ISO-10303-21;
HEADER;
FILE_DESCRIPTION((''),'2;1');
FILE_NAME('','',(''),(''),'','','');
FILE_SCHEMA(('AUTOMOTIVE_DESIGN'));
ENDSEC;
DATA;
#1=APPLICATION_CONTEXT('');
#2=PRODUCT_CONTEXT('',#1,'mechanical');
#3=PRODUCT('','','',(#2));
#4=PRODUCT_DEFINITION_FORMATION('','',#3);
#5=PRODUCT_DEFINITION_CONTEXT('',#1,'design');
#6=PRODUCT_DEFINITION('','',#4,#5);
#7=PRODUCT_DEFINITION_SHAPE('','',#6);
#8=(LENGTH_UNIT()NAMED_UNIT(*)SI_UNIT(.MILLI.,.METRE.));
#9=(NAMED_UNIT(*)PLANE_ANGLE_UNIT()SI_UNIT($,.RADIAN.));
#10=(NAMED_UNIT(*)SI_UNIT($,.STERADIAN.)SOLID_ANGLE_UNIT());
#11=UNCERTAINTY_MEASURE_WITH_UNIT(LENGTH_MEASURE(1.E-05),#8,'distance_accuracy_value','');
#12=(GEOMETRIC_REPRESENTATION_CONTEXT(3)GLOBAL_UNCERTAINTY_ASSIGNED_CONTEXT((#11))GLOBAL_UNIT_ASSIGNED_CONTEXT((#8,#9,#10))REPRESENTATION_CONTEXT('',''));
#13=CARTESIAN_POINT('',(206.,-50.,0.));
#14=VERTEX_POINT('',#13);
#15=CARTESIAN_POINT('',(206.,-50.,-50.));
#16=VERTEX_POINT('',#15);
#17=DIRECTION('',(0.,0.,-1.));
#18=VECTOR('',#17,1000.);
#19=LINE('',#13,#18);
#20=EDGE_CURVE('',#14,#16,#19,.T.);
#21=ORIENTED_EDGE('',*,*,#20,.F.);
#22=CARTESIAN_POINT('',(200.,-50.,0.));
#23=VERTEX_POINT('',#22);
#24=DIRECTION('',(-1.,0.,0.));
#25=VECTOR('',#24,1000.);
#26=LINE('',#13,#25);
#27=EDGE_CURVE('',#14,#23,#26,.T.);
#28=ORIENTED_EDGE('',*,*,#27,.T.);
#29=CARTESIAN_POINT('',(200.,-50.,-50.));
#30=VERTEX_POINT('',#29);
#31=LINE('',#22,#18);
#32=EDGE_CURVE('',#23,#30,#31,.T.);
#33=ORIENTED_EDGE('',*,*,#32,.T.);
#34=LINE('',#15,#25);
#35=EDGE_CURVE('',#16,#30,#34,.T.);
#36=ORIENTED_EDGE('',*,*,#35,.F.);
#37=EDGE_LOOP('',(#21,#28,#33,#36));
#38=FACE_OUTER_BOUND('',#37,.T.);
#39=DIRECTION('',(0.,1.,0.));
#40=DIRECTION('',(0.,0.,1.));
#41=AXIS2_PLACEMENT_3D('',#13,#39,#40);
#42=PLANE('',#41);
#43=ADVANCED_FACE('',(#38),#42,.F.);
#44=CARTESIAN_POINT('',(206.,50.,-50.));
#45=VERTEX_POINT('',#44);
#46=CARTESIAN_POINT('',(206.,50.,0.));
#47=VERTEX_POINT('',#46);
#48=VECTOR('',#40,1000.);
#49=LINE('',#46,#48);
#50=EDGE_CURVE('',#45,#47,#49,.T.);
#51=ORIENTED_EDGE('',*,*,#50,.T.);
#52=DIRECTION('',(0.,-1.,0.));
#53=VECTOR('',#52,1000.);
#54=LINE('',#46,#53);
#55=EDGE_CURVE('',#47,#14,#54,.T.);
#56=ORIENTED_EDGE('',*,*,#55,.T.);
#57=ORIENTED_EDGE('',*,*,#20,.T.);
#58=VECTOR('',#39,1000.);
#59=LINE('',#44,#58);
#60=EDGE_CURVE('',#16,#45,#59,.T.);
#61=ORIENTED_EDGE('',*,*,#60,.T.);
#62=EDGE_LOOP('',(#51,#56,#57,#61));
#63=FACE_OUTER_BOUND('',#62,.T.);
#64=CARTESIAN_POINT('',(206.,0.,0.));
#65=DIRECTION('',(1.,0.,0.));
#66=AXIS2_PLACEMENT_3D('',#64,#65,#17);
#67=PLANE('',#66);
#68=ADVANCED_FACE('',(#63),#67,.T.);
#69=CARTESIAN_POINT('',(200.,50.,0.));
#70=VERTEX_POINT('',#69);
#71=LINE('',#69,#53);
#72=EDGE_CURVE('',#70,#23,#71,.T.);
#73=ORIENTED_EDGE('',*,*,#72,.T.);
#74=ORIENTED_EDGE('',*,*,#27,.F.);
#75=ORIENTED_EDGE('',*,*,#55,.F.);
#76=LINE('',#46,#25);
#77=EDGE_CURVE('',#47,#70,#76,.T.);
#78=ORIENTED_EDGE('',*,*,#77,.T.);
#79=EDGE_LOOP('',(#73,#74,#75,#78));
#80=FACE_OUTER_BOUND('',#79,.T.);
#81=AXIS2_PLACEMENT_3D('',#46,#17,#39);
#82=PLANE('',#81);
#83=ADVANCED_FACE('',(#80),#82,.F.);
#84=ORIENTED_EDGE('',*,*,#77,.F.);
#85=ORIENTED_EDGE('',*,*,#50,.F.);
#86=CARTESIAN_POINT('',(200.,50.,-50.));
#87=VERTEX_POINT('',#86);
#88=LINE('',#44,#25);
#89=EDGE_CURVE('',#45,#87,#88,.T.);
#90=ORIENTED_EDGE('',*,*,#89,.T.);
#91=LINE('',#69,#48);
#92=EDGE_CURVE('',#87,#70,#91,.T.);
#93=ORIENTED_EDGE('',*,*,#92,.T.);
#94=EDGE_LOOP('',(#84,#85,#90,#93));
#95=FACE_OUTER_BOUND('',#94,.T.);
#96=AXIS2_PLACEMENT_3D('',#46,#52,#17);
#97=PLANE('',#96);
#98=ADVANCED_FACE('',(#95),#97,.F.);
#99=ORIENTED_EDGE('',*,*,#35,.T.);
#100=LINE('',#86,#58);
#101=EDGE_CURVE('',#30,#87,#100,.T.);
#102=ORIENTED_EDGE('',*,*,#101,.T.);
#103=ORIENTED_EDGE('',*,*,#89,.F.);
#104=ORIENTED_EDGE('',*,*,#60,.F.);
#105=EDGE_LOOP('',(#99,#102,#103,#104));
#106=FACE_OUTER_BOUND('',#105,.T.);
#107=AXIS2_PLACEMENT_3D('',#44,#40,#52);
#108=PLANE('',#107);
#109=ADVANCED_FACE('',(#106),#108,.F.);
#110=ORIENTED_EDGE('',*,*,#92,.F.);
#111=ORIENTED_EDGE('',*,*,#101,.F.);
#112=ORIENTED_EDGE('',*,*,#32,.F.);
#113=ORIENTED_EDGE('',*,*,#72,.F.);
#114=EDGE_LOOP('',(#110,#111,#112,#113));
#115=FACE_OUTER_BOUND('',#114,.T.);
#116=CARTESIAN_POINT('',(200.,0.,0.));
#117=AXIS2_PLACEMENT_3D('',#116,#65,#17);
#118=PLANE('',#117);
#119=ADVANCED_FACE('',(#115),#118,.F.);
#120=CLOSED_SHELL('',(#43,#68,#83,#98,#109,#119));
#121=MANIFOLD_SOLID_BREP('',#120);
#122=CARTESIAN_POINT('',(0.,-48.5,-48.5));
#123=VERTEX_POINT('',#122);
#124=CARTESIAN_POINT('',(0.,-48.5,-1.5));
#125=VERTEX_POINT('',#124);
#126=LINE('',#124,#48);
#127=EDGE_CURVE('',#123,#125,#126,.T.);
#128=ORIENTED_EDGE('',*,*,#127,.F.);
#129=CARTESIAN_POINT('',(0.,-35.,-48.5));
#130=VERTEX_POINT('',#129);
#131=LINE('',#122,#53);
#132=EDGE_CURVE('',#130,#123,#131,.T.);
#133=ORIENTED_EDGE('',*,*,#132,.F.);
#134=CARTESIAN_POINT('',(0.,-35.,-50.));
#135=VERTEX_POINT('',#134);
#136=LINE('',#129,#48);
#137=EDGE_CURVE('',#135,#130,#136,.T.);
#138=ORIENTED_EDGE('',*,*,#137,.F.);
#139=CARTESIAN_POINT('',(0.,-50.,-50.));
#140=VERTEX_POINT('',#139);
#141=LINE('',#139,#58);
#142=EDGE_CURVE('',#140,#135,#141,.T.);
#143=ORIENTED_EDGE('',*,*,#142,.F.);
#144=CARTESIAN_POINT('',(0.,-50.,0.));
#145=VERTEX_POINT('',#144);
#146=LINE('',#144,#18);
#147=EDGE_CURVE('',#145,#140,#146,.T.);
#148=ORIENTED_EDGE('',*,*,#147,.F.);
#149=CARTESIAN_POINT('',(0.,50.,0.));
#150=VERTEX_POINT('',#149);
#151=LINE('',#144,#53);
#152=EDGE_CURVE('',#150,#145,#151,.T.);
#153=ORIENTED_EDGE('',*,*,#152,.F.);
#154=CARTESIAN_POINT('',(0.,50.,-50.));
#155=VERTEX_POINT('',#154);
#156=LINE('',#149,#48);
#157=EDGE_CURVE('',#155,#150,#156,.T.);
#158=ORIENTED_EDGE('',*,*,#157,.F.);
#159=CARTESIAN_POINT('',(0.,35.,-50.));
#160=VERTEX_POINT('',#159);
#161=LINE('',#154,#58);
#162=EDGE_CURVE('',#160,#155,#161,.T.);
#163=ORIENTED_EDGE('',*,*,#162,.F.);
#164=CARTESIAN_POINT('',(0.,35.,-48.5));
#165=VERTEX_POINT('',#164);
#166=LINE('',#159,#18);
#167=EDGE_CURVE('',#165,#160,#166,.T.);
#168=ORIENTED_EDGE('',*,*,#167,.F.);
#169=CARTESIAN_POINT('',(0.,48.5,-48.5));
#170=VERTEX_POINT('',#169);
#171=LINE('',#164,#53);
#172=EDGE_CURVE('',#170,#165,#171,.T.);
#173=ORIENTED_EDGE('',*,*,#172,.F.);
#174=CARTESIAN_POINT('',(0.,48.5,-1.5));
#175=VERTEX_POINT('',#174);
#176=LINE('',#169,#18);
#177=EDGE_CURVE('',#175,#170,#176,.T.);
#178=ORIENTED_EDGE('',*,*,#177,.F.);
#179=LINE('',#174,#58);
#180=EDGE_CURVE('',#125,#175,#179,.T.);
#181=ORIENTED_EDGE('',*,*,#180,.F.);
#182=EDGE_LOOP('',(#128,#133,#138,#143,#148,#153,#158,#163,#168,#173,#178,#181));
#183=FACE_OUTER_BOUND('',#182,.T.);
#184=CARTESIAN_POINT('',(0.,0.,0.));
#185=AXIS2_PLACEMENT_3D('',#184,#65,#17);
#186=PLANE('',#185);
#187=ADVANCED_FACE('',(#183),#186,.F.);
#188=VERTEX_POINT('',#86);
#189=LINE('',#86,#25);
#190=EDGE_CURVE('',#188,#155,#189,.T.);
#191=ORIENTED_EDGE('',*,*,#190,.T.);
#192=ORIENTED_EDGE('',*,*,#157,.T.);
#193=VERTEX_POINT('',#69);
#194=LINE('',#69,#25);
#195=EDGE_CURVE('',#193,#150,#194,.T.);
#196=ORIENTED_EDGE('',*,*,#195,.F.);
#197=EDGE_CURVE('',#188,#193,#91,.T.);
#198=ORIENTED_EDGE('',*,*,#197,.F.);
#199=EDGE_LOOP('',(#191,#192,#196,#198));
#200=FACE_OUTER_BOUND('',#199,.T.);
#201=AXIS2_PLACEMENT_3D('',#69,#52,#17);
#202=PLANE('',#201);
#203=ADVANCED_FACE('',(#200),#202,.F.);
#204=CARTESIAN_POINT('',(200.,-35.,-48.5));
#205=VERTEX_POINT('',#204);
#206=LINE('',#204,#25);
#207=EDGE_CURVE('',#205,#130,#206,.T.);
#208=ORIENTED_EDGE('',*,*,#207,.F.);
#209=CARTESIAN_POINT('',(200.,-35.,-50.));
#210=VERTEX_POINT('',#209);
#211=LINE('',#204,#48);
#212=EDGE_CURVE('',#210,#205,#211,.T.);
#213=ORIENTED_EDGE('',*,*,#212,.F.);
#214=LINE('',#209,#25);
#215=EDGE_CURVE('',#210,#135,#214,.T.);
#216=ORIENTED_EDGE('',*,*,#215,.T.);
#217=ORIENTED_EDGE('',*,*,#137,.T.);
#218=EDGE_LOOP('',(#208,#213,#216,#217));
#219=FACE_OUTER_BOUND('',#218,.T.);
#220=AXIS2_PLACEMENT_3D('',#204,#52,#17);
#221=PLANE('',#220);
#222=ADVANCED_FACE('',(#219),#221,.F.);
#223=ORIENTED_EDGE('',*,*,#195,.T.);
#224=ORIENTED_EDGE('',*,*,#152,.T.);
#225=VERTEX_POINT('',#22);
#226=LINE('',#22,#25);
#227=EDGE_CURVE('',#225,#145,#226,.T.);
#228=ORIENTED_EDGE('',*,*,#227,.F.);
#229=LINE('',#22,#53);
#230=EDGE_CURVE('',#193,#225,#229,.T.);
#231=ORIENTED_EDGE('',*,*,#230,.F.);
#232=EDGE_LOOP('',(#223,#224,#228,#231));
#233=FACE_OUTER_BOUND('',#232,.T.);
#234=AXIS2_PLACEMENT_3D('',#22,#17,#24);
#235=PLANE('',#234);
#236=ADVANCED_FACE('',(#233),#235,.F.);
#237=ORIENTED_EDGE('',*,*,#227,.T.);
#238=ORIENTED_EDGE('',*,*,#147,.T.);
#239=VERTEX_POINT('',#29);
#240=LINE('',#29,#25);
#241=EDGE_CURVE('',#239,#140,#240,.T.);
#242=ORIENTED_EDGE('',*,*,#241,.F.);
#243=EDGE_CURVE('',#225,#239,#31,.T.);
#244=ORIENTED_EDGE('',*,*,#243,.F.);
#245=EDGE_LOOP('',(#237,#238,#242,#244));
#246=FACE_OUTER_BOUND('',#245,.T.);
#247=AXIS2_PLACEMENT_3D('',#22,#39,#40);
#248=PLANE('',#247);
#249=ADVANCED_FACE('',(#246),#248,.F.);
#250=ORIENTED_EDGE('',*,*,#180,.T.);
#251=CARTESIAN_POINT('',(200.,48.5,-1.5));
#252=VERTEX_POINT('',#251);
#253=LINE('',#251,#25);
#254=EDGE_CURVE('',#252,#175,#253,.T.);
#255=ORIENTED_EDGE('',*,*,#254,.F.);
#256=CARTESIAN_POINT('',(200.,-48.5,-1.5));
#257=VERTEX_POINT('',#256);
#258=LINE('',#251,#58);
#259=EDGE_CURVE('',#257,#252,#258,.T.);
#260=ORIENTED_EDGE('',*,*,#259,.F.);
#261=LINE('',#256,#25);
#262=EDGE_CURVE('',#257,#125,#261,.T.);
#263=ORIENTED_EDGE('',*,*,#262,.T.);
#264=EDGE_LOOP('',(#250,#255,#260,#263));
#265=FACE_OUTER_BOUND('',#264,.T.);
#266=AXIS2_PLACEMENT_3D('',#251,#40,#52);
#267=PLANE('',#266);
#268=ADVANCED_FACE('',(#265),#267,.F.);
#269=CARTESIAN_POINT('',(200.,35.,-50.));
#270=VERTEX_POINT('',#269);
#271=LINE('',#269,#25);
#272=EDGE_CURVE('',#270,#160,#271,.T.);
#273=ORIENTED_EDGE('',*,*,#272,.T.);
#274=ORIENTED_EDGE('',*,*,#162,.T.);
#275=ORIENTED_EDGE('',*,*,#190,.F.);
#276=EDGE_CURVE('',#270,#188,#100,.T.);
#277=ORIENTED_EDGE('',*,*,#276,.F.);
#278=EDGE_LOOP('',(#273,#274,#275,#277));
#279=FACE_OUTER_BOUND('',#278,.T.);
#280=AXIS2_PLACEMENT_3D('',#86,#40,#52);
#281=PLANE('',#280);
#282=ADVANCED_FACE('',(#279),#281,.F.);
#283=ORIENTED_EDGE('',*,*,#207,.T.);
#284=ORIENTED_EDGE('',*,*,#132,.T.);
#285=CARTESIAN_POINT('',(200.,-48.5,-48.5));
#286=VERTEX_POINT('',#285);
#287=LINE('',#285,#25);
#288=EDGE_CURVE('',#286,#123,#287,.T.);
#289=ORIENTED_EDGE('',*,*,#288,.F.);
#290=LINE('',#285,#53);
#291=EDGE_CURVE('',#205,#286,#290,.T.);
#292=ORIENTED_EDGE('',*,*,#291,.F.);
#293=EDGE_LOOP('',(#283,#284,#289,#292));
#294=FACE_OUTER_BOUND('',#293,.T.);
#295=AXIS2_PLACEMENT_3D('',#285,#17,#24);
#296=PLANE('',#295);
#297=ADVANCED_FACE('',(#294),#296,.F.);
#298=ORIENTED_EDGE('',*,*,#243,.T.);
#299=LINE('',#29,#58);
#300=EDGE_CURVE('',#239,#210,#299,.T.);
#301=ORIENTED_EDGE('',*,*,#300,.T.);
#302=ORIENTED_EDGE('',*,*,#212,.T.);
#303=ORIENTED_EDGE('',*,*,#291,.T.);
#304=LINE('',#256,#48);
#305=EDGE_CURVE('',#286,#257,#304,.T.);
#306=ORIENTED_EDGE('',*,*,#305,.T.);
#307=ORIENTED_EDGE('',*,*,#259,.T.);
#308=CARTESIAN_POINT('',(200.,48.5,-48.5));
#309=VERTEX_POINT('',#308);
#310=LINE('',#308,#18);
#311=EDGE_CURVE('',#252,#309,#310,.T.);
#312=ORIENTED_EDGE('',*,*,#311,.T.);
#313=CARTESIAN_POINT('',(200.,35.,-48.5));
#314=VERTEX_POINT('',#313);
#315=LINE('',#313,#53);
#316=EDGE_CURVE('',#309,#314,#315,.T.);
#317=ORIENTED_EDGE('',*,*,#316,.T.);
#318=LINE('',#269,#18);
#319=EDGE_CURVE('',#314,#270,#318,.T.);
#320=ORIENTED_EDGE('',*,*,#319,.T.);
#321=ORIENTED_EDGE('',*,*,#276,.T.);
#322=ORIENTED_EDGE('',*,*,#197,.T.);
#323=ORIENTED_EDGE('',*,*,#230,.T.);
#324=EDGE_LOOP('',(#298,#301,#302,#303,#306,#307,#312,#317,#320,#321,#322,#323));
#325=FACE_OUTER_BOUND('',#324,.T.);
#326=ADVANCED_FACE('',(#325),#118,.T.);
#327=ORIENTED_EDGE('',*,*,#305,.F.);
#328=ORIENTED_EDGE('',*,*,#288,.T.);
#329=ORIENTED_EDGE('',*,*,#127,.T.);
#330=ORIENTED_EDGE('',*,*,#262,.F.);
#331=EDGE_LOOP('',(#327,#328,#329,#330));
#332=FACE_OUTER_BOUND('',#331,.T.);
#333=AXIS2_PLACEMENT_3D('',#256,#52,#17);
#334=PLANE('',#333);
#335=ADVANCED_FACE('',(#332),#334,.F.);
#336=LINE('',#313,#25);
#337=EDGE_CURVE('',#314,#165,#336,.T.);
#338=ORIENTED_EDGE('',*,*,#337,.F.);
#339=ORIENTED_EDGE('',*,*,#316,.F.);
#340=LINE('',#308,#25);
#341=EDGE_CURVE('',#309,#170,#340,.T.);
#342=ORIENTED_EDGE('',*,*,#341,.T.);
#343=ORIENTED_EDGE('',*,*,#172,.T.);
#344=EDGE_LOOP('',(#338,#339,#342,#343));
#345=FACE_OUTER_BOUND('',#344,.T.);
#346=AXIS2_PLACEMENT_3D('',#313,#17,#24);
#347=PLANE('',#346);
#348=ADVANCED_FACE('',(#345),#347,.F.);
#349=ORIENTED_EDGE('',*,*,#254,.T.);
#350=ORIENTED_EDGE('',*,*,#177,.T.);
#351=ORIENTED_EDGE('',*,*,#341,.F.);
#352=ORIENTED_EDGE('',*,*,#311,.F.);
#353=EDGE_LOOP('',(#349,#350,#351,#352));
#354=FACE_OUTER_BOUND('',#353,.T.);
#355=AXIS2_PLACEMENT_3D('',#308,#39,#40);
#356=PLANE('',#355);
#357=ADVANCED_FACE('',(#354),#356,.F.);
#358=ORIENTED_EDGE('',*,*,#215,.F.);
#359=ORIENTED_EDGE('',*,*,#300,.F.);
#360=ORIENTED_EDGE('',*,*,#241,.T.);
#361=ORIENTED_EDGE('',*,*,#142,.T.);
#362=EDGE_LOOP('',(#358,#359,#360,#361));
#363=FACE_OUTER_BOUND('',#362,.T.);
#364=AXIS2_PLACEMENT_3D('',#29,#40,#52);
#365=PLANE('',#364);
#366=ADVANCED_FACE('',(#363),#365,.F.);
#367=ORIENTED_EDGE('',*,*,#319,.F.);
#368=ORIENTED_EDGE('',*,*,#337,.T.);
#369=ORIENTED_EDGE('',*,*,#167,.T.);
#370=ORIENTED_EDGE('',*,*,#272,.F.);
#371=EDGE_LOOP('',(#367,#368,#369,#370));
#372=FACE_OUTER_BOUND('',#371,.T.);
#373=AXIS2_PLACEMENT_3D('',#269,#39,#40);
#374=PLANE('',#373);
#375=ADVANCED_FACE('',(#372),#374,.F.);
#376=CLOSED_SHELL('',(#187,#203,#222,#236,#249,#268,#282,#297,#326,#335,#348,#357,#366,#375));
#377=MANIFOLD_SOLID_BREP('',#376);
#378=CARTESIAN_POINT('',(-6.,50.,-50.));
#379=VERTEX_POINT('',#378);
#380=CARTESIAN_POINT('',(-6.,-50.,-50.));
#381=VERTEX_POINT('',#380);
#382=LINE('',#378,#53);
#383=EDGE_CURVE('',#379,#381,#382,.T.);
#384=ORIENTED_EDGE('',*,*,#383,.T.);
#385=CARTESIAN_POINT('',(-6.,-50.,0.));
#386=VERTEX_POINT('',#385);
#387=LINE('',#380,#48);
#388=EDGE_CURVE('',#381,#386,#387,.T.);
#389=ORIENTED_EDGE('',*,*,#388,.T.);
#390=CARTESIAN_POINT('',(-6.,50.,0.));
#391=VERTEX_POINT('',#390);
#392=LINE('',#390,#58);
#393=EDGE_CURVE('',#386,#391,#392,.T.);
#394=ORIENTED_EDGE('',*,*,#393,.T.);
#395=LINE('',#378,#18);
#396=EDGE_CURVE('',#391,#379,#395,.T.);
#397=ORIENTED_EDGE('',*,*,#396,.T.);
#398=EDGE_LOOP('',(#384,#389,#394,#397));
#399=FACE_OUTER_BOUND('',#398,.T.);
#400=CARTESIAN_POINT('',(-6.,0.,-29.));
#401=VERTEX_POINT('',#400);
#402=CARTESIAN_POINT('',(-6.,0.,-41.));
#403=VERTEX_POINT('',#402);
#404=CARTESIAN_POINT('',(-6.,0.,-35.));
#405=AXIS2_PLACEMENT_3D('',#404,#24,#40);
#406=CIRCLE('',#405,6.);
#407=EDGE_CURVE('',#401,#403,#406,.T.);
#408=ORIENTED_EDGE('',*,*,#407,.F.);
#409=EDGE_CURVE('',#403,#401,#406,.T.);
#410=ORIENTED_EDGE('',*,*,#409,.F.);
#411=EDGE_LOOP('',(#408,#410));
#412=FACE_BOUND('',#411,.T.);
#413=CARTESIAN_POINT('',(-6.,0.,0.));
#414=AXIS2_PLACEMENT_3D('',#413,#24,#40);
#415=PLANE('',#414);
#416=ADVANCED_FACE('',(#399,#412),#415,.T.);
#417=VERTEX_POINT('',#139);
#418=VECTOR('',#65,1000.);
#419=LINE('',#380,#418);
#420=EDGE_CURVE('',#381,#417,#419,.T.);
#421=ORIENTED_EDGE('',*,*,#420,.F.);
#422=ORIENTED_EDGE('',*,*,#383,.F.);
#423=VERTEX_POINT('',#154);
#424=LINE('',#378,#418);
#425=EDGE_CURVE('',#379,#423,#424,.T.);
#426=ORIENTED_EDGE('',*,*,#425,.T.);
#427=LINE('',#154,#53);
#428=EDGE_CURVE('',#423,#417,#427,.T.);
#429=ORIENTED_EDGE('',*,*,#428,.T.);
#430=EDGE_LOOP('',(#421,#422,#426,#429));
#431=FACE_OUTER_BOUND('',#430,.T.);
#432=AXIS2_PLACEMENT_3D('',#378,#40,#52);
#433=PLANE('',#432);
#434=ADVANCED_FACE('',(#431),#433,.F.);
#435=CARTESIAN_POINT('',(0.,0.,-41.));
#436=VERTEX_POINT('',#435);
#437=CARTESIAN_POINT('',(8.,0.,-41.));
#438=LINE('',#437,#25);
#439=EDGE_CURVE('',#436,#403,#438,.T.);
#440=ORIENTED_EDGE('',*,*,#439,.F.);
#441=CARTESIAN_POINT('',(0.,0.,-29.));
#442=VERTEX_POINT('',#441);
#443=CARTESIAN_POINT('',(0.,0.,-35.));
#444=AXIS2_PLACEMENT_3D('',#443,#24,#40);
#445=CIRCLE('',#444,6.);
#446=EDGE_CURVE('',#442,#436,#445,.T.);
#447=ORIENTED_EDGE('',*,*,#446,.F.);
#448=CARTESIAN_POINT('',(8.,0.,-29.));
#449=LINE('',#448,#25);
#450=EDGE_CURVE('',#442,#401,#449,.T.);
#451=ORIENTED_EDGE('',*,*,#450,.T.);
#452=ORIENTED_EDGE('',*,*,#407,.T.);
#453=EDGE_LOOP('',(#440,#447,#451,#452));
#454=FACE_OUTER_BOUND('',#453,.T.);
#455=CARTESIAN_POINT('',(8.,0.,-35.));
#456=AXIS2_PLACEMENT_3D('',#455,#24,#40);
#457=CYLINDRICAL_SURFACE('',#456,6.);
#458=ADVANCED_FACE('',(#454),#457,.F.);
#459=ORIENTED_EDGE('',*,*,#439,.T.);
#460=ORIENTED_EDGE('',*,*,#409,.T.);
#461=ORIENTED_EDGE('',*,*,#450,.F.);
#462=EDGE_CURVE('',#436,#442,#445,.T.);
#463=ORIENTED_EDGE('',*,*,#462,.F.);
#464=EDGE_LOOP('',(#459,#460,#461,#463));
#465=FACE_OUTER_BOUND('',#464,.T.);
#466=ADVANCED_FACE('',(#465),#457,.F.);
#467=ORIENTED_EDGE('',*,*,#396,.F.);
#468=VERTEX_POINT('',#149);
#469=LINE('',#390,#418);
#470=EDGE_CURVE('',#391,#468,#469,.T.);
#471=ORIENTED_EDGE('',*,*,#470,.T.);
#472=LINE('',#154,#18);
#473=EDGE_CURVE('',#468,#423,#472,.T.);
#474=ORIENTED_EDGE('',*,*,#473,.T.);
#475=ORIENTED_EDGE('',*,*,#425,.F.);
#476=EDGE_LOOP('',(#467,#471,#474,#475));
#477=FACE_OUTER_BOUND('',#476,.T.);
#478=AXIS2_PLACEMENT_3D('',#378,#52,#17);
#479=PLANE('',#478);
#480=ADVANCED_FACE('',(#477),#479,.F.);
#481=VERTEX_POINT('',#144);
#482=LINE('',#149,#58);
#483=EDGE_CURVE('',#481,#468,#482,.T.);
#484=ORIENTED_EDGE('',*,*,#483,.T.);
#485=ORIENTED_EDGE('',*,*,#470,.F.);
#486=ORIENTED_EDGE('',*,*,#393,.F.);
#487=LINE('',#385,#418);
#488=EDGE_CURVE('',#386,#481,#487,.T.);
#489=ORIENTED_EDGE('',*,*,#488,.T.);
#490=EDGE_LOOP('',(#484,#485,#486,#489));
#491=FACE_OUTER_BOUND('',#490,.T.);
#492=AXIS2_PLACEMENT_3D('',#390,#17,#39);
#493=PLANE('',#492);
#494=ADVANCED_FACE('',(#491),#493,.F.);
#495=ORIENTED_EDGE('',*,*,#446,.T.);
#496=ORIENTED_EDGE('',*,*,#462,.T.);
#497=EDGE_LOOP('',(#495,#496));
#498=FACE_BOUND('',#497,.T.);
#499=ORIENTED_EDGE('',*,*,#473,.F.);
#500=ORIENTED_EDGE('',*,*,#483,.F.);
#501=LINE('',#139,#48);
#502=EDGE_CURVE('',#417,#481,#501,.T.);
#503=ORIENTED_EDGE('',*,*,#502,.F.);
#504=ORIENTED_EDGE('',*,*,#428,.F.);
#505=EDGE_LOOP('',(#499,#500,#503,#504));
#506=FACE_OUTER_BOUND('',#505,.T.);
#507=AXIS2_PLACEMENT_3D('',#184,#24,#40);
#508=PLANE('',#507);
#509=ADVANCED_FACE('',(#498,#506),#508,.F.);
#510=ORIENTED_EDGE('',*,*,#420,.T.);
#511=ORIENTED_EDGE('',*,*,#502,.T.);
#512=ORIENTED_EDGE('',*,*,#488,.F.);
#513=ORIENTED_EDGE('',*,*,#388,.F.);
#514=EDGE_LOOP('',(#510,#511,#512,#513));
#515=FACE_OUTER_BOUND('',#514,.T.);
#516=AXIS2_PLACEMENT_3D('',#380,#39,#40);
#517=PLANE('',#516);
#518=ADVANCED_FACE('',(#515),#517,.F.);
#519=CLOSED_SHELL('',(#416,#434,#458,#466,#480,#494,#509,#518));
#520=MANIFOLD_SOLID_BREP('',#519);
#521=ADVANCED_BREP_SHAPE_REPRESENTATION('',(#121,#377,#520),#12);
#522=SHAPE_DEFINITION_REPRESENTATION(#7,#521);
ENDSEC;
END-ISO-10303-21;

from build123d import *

# Parameters (mm, degrees)
C_CHANNEL_C80X40X15X1_5_1_DEPTH = 200
SKETCH12_W                      = 50
SKETCH12_H                      = 100
BOSS_EXTRUDE1_DEPTH             = 6
SKETCH13_W                      = 50
SKETCH13_H                      = 100
BOSS_EXTRUDE2_DEPTH             = 6
SKETCH14_R                      = 6
CUT_EXTRUDE1_DEPTH              = 14


with BuildPart() as part:
    # Sketch11 → C-channel C80X40X15X1.5(1) (new body)
    with BuildSketch(Plane(origin=(0, 0, 0), x_dir=(0, 0, -1), z_dir=(1, 0, 0))):
        Polygon((0, -50), (0, 50), (50, 50), (50, 35), (48.5, 35), (48.5, 48.5), (1.5, 48.5), (1.5, -48.5), (48.5, -48.5), (48.5, -35), (50, -35), (50, -50), align=None)
    extrude(amount=C_CHANNEL_C80X40X15X1_5_1_DEPTH)


with BuildPart() as body_2:
    # Sketch12 → Boss-Extrude1 (new body)
    with BuildSketch(Plane(origin=(200, 0, 0), x_dir=(0, 0, -1), z_dir=(1, 0, 0))):
        with Locations((25, 0)):
            Rectangle(SKETCH12_W, SKETCH12_H)
    extrude(amount=BOSS_EXTRUDE1_DEPTH)


with BuildPart() as body_3:
    # Sketch13 → Boss-Extrude2 (new body)
    with BuildSketch(Plane.ZY):
        with Locations((-25, 0)):
            Rectangle(SKETCH13_W, SKETCH13_H)
    extrude(amount=BOSS_EXTRUDE2_DEPTH)

    # Sketch14 → Cut-Extrude1 (cut)
    with BuildSketch(Plane.ZY.offset(6)):
        with Locations((-35, 0)):
            Circle(SKETCH14_R)
    extrude(amount=-CUT_EXTRUDE1_DEPTH, mode=Mode.SUBTRACT)


solid = Compound([part.part, body_2.part, body_3.part])
